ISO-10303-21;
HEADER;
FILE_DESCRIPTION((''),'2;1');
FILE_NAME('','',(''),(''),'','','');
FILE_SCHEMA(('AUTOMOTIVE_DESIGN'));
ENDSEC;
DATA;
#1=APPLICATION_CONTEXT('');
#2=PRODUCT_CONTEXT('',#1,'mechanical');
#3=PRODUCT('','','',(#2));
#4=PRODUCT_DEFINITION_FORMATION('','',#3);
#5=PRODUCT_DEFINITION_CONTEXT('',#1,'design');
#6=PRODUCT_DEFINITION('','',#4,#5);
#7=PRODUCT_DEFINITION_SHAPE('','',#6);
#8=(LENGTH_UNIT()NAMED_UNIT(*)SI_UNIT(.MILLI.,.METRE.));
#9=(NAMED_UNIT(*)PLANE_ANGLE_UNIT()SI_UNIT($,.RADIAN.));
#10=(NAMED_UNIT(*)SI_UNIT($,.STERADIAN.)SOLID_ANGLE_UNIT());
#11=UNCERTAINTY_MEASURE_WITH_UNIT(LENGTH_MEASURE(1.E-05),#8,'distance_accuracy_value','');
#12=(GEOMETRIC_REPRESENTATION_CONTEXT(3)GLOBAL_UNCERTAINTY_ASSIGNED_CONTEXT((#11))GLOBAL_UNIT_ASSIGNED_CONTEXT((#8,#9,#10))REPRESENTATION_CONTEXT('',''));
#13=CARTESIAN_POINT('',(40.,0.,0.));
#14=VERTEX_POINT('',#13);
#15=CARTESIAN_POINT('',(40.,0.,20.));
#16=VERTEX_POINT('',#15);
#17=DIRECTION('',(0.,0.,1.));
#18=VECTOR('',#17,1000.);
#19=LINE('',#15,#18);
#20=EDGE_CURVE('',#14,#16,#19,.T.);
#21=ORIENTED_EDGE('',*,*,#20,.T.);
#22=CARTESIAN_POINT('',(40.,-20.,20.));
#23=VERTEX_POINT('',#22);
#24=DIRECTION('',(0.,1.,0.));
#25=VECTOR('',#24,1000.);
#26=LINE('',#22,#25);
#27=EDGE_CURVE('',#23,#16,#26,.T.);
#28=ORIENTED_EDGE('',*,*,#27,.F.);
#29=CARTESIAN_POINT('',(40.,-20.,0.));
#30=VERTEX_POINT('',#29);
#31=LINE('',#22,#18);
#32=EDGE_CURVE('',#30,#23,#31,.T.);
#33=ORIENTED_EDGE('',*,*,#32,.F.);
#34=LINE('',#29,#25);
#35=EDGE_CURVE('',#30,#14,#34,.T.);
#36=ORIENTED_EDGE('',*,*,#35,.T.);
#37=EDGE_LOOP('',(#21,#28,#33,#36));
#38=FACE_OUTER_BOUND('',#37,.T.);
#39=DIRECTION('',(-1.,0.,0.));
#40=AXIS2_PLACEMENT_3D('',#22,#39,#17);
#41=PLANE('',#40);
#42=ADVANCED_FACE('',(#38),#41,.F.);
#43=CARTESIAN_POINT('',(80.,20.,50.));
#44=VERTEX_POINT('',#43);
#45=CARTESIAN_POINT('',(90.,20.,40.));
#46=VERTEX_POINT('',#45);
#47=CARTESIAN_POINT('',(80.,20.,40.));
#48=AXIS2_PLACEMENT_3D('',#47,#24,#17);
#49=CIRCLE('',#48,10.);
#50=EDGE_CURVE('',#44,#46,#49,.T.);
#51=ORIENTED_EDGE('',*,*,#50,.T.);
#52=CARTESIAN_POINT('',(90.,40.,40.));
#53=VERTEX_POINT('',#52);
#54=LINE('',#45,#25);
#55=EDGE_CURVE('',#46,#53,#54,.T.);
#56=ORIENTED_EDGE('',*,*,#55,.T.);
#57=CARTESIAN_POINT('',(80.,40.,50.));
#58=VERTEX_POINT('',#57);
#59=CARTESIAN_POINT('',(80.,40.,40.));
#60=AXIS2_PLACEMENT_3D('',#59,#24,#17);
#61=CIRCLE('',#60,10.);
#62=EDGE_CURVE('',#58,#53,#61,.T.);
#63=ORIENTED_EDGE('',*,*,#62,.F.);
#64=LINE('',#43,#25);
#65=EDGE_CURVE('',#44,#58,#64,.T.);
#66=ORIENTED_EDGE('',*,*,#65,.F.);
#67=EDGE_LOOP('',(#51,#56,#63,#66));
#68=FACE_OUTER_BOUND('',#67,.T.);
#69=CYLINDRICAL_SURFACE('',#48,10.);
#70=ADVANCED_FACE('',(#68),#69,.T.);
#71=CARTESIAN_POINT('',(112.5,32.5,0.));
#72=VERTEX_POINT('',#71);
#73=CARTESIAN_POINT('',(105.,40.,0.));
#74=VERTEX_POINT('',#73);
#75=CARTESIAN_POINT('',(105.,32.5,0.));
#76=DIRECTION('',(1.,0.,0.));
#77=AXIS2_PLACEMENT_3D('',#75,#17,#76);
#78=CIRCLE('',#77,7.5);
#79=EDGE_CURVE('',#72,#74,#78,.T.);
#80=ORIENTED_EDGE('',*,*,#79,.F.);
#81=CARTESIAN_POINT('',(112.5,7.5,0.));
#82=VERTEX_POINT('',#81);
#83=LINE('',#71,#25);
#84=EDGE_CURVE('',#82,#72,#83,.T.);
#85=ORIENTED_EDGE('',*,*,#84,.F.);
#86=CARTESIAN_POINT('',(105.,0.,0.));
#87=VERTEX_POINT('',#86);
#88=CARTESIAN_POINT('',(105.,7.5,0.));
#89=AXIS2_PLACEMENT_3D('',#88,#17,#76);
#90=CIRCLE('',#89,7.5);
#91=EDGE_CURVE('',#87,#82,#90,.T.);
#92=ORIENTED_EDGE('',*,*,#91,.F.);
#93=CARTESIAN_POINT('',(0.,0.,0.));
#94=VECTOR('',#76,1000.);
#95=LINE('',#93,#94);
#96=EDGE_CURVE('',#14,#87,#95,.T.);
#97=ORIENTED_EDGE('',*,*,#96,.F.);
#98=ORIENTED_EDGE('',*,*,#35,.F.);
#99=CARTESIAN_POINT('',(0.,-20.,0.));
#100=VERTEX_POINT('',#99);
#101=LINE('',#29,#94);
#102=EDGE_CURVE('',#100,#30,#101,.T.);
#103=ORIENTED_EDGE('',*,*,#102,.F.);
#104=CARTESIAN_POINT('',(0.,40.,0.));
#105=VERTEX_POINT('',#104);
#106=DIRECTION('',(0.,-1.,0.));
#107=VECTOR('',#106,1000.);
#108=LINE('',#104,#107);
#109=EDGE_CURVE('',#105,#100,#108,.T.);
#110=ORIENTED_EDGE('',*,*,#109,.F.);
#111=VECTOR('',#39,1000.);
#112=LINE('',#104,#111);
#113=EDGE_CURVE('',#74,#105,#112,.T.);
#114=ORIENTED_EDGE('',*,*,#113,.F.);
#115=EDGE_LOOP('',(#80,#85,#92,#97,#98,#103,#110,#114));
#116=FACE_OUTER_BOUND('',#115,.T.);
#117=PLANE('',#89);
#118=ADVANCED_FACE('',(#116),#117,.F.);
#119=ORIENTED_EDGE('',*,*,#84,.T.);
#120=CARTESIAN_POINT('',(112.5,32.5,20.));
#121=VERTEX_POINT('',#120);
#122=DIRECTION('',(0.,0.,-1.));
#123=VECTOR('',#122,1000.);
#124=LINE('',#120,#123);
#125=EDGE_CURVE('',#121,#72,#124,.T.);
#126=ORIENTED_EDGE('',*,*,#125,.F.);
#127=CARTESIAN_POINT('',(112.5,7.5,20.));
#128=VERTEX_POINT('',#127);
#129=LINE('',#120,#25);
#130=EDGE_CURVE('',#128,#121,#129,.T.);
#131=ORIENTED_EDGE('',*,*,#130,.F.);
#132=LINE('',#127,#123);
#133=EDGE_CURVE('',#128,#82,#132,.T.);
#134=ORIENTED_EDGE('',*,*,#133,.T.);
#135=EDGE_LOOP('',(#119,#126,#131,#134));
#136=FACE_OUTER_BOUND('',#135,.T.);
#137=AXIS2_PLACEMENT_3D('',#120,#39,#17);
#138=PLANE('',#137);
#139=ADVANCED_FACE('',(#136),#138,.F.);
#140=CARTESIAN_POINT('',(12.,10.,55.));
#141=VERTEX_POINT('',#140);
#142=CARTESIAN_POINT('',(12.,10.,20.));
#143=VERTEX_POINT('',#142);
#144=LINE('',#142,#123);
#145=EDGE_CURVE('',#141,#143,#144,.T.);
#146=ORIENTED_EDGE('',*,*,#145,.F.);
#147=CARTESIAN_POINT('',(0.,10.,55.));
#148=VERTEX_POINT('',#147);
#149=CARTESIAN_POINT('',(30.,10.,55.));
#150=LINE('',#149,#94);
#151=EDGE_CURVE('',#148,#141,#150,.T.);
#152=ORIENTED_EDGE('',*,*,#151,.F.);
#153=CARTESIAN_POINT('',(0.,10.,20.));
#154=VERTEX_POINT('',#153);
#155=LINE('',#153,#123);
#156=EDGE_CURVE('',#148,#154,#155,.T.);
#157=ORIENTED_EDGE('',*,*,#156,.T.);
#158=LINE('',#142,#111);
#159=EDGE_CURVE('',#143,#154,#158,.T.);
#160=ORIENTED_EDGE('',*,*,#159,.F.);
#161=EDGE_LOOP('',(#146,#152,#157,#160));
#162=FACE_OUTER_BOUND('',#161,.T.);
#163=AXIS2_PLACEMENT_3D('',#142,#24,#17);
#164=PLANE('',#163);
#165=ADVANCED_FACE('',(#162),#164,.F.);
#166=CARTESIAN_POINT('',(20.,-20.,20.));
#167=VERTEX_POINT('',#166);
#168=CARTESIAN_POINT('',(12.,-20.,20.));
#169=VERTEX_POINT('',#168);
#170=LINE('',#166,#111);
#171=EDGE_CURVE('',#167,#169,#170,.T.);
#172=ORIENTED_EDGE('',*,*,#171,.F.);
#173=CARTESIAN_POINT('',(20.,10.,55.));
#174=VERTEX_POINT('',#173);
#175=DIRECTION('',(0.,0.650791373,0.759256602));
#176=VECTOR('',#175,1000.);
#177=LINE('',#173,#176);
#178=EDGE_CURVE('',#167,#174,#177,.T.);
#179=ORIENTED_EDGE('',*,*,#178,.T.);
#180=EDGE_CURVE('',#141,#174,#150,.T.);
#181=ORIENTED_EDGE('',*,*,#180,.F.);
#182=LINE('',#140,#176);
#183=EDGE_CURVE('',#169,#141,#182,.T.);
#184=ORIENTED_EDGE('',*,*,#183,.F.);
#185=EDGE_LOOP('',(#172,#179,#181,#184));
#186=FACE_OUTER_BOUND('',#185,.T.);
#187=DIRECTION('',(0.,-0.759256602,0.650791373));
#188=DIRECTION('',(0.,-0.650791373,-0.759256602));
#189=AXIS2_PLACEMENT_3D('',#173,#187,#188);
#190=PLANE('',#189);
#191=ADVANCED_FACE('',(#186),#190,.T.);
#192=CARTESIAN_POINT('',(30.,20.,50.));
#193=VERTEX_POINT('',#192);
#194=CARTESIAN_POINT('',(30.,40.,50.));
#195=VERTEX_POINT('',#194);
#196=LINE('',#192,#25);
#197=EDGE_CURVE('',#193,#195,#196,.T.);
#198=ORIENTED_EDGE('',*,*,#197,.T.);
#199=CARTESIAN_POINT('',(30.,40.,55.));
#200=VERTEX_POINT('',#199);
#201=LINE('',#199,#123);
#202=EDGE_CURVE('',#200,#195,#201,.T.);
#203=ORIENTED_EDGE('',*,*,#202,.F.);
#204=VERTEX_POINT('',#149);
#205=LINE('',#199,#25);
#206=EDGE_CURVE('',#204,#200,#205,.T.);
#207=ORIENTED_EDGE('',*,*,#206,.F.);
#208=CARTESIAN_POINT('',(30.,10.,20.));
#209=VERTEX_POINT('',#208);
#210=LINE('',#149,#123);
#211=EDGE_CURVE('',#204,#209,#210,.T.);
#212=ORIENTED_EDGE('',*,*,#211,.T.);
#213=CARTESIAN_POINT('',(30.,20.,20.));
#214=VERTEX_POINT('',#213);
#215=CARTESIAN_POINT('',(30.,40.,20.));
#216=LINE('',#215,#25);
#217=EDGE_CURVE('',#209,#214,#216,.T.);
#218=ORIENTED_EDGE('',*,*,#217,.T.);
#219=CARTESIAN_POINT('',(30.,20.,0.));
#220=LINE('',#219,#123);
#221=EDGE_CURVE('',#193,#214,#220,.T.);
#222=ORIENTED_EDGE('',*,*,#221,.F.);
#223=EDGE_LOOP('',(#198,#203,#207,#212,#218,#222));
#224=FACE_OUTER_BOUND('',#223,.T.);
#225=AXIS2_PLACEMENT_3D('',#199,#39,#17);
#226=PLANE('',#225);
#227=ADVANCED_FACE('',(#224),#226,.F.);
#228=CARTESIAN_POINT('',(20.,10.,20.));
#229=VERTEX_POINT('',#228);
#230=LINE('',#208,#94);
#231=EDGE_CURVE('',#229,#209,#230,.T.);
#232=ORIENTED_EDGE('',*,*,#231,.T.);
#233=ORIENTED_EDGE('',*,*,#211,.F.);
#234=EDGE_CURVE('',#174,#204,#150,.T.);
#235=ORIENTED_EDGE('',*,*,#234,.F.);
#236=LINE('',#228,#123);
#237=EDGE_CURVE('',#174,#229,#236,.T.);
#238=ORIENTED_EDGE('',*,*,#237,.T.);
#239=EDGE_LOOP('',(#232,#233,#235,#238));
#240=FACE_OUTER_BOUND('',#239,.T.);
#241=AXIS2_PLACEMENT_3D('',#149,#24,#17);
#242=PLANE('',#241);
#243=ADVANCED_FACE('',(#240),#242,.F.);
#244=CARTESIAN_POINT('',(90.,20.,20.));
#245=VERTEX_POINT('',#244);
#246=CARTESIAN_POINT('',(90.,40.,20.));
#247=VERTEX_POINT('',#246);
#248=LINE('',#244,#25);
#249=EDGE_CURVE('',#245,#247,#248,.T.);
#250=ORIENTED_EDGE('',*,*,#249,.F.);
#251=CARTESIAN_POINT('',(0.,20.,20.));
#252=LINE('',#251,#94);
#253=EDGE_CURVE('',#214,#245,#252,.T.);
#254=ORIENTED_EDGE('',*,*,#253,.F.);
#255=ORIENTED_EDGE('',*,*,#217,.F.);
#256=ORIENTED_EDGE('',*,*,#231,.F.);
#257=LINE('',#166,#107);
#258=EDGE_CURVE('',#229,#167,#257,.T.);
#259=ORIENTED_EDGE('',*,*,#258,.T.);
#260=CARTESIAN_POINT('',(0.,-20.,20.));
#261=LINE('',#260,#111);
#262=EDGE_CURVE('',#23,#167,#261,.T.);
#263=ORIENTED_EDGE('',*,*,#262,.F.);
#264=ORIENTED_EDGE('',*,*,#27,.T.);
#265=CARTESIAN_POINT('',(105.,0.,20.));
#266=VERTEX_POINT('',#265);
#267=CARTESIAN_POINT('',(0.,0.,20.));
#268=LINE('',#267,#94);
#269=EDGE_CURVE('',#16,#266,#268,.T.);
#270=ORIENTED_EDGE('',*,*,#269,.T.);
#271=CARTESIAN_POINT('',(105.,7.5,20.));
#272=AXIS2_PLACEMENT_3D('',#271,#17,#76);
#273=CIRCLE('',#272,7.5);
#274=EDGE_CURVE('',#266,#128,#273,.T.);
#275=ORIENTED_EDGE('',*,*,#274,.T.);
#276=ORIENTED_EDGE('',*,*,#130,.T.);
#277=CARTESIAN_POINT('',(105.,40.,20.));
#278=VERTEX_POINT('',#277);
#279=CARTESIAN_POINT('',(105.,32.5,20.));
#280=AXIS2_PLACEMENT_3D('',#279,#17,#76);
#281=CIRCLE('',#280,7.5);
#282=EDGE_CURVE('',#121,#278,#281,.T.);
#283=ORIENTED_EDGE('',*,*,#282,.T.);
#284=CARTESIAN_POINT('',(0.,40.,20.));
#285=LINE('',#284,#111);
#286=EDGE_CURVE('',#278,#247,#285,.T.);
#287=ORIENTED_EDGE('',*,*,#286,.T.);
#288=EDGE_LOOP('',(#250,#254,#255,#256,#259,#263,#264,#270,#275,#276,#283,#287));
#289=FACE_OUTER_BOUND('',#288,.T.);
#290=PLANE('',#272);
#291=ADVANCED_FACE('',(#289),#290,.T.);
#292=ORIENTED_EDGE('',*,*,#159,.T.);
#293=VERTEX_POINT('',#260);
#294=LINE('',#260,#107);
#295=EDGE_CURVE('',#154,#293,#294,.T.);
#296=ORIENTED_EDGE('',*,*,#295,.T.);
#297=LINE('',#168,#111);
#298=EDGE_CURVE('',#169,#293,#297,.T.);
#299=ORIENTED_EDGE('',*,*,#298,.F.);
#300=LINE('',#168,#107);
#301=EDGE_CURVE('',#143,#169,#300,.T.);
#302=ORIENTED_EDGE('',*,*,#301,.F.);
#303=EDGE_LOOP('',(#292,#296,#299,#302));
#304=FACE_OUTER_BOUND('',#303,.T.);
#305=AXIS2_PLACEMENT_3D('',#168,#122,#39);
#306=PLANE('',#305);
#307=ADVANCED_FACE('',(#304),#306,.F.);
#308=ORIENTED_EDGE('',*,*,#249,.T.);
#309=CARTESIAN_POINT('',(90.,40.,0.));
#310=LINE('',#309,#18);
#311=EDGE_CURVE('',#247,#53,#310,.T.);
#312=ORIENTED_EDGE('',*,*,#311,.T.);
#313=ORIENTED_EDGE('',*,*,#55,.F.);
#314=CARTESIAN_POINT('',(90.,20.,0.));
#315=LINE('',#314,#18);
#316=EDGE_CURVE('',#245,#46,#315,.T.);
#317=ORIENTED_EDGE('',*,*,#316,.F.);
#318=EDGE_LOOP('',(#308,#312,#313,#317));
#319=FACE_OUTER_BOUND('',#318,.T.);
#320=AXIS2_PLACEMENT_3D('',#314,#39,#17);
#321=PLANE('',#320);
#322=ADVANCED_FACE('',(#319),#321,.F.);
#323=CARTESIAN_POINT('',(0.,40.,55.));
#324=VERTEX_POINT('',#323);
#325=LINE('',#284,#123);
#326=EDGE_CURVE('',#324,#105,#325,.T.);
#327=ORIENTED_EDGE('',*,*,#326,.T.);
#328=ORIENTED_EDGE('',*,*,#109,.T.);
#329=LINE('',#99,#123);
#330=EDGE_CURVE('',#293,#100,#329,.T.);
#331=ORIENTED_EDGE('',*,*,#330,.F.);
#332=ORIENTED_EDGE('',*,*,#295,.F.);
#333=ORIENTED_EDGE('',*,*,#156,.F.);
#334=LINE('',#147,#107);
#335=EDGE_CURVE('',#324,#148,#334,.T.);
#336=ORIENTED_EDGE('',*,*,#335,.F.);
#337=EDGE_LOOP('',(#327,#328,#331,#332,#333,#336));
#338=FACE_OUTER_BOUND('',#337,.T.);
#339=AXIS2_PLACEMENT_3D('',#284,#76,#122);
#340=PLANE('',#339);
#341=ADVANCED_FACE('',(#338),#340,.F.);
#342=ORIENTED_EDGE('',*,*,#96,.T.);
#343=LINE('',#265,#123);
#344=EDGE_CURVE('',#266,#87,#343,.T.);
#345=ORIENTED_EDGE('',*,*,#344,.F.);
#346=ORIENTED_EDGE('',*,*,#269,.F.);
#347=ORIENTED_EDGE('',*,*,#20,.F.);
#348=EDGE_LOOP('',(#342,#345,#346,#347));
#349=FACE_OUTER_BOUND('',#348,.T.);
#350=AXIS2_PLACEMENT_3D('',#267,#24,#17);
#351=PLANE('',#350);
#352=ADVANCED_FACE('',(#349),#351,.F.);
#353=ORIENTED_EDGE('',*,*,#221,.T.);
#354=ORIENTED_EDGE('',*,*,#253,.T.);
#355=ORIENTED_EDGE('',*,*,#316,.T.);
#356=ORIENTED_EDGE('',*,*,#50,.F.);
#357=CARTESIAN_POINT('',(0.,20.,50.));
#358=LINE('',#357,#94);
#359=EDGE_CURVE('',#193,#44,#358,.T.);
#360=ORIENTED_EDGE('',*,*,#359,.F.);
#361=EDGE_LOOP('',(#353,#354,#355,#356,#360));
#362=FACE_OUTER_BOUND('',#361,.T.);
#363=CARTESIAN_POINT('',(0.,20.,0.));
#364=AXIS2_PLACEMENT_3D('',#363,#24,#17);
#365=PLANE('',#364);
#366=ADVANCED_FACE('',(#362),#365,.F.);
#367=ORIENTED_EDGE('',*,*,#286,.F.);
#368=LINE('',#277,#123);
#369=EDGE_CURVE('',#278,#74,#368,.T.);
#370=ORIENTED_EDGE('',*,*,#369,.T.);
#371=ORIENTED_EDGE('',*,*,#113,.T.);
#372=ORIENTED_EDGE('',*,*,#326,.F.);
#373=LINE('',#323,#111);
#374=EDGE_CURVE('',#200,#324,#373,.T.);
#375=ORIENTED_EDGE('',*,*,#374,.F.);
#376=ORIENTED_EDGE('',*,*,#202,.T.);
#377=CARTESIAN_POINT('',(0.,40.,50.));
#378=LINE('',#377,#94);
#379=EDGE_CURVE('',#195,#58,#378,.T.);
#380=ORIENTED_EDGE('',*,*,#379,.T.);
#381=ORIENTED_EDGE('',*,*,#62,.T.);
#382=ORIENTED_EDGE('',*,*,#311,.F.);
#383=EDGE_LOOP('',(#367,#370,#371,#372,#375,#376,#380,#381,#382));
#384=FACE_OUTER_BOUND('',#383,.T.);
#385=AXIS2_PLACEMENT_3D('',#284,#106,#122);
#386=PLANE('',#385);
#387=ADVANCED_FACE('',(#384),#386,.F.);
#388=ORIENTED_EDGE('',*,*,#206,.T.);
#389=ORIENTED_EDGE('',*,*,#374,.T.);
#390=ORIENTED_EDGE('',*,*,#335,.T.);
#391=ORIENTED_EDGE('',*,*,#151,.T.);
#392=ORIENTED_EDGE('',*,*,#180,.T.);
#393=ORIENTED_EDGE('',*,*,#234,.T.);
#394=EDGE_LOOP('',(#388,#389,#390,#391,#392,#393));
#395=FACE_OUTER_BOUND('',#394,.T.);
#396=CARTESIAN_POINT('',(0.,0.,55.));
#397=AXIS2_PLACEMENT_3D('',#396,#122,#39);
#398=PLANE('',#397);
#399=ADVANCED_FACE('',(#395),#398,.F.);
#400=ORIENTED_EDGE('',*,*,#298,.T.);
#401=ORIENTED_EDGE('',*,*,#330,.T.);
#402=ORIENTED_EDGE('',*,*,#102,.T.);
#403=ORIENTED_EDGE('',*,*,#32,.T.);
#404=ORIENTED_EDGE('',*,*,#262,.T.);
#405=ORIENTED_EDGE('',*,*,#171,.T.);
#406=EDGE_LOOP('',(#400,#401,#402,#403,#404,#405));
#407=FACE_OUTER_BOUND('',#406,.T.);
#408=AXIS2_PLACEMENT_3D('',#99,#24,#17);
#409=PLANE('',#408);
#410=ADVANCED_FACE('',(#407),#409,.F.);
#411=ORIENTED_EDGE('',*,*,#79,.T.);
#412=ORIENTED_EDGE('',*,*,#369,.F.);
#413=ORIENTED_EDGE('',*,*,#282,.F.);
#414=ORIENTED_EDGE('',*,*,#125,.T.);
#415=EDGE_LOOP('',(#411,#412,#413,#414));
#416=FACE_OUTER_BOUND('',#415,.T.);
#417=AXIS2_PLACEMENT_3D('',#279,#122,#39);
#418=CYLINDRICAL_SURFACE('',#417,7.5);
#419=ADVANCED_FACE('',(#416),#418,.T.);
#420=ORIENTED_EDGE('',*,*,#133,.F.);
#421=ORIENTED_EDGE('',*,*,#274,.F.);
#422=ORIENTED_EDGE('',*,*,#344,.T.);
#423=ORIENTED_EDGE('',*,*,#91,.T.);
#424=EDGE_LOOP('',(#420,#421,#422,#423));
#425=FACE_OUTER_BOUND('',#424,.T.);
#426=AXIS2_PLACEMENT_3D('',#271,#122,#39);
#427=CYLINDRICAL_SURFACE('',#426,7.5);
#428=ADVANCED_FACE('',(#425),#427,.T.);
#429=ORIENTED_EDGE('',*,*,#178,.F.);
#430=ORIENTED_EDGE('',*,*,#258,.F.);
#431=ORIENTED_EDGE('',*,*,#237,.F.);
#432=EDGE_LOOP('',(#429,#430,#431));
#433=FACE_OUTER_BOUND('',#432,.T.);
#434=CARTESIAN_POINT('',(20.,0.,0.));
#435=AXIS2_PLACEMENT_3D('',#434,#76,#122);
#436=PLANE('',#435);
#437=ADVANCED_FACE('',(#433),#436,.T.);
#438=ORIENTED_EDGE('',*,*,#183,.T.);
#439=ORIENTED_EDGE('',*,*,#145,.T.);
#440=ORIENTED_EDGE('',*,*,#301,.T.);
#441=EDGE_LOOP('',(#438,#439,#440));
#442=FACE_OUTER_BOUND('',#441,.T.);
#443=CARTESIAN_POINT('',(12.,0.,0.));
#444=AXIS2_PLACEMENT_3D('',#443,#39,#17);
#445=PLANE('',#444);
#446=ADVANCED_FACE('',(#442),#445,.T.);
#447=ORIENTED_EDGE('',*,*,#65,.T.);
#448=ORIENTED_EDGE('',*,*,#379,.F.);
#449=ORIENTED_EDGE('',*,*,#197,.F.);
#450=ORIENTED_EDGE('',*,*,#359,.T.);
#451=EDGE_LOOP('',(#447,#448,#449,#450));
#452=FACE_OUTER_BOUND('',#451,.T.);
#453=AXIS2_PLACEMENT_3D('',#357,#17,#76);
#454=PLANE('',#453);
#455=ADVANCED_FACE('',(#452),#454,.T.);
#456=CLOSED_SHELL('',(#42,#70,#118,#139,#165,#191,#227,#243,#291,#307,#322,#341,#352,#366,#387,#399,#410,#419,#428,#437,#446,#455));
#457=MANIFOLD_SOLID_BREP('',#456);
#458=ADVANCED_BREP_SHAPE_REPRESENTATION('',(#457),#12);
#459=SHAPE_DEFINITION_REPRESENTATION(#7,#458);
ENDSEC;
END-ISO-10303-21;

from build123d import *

# Parameters (mm, degrees)
BASE_BLOCK_DEPTH          = 20
SIDE_BLOCK_SKETCH_W       = 40
SIDE_BLOCK_SKETCH_H       = 20
SIDE_BLOCK_DEPTH          = 20
LONG_BLOCK_SKETCH_W       = 30
LONG_BLOCK_SKETCH_H       = 30
LONG_BLOCK_DEPTH          = 35
ROUNDED_END_BOSS_DEPTH    = 20
TRIANGULAR_GUSSET_DEPTH   = 20
TRIANGULAR_CUT_12MM_DEPTH = 12


with BuildPart() as part:
    # Base Block Sketch → Base Block (new body)
    with BuildSketch(Plane.XY):
        with BuildLine():
            Line((0, 0), (105, 0))
            ThreePointArc((105, 0), (110.303300859, 2.196699141), (112.5, 7.5))
            Line((112.5, 7.5), (112.5, 32.5))
            ThreePointArc((112.5, 32.5), (110.303300859, 37.803300859), (105, 40))
            Line((105, 40), (0, 40))
            Line((0, 40), (0, 0))
        make_face()
    extrude(amount=BASE_BLOCK_DEPTH)

    # Side Block Sketch → Side Block (add)
    with BuildSketch(Plane.XZ):
        with Locations((20, 10)):
            Rectangle(SIDE_BLOCK_SKETCH_W, SIDE_BLOCK_SKETCH_H)
    extrude(amount=SIDE_BLOCK_DEPTH)

    # Long Block Sketch → Long Block (add)
    with BuildSketch(Plane.XY.offset(20)):
        with Locations((15, 25)):
            Rectangle(LONG_BLOCK_SKETCH_W, LONG_BLOCK_SKETCH_H)
    extrude(amount=LONG_BLOCK_DEPTH)

    # Rounded End Sketch → Rounded End Boss (add)
    with BuildSketch(Plane(origin=(0, 40, 0), x_dir=(1, 0, 0), z_dir=(0, 1, 0))):
        with BuildLine():
            Line((80, -20), (30, -20))
            Line((30, -20), (30, -50))
            Line((30, -50), (80, -50))
            ThreePointArc((80, -50), (87.071067812, -47.071067812), (90, -40))
            Line((90, -40), (90, -20))
            Line((90, -20), (80, -20))
        make_face()
    extrude(amount=-ROUNDED_END_BOSS_DEPTH)

    # Triangular Gusset Sketch → Triangular Gusset (add)
    with BuildSketch(Plane.ZY):
        Polygon((20, 10), (55, 10), (20, -20), align=None)
    extrude(amount=-TRIANGULAR_GUSSET_DEPTH)

    # Triangular Cut Sketch → Triangular Cut 12mm (cut)
    with BuildSketch(Plane.ZY):
        Polygon((55, 10), (20, -20), (20, 10), align=None)
    extrude(amount=-TRIANGULAR_CUT_12MM_DEPTH, mode=Mode.SUBTRACT)


solid = part.part
